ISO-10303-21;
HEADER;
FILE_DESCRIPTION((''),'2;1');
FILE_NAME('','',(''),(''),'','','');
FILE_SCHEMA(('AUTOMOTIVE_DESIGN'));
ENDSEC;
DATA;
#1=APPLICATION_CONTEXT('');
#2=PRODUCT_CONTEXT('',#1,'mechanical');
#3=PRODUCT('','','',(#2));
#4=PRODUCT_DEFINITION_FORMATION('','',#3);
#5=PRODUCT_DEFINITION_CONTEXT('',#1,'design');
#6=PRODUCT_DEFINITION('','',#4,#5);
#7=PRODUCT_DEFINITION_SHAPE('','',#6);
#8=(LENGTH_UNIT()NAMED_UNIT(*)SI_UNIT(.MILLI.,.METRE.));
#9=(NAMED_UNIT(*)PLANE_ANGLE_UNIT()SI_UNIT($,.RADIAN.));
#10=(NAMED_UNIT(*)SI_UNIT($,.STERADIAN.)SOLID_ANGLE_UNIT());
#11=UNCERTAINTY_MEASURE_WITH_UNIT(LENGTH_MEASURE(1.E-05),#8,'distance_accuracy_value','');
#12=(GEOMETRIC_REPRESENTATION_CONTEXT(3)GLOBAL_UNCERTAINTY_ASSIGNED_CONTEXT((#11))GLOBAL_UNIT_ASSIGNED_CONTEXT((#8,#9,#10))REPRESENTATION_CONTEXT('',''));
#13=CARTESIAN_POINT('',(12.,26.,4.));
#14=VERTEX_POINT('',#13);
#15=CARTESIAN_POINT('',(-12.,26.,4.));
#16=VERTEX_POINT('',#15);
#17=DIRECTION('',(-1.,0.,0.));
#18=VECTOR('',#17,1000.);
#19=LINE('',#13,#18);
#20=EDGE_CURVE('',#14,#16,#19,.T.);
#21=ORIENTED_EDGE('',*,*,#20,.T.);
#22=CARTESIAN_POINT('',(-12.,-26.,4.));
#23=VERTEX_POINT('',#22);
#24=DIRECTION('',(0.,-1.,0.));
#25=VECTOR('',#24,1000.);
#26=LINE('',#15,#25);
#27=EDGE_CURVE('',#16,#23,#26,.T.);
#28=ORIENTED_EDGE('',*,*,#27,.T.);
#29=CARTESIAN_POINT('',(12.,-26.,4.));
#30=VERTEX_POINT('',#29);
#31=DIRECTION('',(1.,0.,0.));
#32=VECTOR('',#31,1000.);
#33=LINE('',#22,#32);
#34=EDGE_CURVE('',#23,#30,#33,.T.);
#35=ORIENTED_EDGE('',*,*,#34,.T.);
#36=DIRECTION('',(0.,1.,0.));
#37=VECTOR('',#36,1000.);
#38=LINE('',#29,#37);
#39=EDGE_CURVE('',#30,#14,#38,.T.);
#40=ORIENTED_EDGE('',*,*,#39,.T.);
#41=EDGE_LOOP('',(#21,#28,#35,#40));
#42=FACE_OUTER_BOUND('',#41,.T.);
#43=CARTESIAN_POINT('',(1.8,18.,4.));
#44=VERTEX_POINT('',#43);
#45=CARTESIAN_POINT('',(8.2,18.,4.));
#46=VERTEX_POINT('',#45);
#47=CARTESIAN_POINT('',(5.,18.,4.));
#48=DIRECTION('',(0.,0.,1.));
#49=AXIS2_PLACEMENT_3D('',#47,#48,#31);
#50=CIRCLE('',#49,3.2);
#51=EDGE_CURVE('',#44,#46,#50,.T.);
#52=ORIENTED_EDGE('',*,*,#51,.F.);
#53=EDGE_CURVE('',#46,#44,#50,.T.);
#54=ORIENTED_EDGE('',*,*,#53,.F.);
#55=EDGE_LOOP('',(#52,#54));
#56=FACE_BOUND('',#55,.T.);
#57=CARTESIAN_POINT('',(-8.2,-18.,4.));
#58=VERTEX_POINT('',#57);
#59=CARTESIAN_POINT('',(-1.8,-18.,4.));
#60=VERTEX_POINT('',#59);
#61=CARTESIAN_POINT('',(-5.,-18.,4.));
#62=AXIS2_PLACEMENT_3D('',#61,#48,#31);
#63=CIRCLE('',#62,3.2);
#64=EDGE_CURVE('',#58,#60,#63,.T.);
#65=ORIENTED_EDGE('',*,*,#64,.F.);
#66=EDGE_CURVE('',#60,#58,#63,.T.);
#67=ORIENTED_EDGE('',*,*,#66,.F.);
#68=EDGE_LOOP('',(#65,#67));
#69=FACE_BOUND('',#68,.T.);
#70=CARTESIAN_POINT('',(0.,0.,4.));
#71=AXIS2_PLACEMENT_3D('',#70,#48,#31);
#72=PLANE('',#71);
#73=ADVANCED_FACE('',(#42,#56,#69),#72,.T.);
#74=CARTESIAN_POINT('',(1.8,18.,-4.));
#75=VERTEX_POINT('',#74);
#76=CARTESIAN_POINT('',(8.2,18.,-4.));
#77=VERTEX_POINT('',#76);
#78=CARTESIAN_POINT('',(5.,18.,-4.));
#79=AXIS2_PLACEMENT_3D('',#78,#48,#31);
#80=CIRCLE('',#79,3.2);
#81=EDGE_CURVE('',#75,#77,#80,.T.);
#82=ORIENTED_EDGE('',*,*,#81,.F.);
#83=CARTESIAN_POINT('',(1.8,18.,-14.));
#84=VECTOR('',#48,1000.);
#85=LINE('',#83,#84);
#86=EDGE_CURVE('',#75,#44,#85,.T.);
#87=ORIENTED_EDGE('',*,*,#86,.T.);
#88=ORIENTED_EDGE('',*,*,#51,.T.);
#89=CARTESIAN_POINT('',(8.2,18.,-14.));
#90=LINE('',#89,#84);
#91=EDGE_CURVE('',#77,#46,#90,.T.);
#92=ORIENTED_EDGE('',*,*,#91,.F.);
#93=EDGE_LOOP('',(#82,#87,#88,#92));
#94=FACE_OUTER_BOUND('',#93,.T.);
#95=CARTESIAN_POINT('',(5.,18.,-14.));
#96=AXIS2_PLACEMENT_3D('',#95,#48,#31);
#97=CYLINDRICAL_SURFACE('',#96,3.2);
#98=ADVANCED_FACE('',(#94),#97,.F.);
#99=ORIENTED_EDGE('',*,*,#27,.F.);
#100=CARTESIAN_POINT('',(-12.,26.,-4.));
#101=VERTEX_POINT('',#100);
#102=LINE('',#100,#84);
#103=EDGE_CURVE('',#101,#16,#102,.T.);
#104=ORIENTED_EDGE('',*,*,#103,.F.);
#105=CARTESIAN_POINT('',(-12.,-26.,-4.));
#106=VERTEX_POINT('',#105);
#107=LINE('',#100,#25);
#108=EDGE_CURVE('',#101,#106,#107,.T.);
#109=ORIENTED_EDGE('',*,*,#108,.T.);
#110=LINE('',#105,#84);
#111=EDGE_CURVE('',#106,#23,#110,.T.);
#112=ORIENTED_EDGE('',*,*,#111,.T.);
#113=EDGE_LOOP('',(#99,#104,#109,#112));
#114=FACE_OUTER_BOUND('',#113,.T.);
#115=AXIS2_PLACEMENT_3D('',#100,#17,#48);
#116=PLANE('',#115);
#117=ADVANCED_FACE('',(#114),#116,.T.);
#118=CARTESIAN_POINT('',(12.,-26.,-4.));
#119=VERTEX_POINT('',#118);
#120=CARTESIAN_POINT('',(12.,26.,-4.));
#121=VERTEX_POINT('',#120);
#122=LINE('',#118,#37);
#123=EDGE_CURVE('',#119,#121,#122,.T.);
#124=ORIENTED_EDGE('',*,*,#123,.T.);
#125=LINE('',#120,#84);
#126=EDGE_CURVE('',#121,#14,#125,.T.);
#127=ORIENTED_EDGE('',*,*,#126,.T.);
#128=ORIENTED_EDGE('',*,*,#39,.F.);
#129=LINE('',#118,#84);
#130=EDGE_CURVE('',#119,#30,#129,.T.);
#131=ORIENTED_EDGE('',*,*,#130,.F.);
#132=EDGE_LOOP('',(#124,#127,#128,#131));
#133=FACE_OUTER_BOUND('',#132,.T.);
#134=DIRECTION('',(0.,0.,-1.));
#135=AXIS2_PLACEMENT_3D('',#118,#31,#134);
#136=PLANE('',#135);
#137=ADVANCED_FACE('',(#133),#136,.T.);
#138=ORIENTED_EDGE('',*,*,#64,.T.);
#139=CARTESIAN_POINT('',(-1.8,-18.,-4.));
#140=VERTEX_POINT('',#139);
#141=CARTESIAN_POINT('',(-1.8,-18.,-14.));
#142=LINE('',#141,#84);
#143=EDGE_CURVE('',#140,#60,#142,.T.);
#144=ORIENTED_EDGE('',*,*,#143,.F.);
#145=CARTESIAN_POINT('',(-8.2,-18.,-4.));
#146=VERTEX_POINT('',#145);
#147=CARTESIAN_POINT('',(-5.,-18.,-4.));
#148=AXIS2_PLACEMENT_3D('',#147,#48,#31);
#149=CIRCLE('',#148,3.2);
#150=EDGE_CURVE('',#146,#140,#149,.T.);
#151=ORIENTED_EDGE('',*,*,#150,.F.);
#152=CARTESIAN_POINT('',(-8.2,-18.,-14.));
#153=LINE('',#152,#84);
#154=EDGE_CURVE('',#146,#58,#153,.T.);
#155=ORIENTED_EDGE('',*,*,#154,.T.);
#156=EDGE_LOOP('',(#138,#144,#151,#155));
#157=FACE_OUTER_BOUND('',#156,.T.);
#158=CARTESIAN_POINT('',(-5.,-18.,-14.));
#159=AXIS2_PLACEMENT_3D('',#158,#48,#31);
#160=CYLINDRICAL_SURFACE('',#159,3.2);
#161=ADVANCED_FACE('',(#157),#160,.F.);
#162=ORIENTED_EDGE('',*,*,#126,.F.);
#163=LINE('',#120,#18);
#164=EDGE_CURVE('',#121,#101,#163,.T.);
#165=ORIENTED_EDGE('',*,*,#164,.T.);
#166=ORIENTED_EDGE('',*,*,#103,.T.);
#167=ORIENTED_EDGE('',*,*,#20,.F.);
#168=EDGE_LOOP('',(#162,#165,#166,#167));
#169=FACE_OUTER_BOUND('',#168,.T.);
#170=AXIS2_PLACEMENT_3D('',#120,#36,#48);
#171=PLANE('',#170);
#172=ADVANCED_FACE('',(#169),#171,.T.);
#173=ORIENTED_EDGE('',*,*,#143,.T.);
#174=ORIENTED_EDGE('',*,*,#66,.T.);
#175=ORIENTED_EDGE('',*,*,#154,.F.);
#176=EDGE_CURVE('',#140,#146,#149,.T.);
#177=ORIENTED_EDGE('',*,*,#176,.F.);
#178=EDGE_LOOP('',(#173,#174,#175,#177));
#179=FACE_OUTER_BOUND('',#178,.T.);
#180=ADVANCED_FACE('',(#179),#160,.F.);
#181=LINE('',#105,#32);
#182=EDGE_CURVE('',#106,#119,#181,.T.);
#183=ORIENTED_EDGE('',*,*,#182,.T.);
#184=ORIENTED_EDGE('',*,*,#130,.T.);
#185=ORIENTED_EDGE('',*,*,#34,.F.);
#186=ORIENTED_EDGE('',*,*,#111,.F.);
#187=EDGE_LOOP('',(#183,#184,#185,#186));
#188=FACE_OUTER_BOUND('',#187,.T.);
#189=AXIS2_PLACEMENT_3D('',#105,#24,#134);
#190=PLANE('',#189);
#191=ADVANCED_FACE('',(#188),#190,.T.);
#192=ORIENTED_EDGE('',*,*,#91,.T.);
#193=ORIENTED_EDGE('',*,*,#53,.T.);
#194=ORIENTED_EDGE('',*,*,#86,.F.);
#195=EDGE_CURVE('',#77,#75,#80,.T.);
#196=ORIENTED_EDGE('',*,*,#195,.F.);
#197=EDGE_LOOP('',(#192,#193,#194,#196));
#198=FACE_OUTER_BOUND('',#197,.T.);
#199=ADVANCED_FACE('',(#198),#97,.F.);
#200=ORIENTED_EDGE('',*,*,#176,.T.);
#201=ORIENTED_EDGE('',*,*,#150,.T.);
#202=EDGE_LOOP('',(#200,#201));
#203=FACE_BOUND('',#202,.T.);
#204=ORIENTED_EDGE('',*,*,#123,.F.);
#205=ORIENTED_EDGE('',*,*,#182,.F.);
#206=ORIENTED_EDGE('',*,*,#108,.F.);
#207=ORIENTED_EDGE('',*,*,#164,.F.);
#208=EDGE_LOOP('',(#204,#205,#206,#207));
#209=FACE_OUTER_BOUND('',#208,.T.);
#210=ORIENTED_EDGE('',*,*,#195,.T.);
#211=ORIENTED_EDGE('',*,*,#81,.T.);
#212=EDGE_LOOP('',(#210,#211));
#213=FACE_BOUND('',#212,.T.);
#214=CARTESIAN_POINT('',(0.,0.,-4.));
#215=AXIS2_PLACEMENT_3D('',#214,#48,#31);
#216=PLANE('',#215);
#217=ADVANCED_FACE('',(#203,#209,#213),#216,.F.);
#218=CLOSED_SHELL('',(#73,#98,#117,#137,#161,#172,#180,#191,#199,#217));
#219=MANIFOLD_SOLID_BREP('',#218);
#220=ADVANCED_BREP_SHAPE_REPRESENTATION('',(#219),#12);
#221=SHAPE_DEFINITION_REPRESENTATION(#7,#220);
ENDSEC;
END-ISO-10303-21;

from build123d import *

# Parameters (mm, degrees)
SKETCH_1_W          = 24
SKETCH_1_H          = 52
EXTRUDE_1_DEPTH     = 4
SKETCH_2_R          = 3.2
CUT_EXTRUDE_1_DEPTH = 14


with BuildPart() as part:
    # 草图1 → 凸台-拉伸1 (new, symmetric)
    with BuildSketch(Plane.XY):
        Rectangle(SKETCH_1_W, SKETCH_1_H)
    extrude(amount=EXTRUDE_1_DEPTH, both=True)

    # 草图2 → 切除-拉伸1 (cut, symmetric)
    with BuildSketch(Plane.XY):
        with Locations((-5, -18)):
            Circle(SKETCH_2_R)
        with Locations((5, 18)):
            Circle(SKETCH_2_R)
    extrude(amount=CUT_EXTRUDE_1_DEPTH, both=True, mode=Mode.SUBTRACT)


solid = part.part
